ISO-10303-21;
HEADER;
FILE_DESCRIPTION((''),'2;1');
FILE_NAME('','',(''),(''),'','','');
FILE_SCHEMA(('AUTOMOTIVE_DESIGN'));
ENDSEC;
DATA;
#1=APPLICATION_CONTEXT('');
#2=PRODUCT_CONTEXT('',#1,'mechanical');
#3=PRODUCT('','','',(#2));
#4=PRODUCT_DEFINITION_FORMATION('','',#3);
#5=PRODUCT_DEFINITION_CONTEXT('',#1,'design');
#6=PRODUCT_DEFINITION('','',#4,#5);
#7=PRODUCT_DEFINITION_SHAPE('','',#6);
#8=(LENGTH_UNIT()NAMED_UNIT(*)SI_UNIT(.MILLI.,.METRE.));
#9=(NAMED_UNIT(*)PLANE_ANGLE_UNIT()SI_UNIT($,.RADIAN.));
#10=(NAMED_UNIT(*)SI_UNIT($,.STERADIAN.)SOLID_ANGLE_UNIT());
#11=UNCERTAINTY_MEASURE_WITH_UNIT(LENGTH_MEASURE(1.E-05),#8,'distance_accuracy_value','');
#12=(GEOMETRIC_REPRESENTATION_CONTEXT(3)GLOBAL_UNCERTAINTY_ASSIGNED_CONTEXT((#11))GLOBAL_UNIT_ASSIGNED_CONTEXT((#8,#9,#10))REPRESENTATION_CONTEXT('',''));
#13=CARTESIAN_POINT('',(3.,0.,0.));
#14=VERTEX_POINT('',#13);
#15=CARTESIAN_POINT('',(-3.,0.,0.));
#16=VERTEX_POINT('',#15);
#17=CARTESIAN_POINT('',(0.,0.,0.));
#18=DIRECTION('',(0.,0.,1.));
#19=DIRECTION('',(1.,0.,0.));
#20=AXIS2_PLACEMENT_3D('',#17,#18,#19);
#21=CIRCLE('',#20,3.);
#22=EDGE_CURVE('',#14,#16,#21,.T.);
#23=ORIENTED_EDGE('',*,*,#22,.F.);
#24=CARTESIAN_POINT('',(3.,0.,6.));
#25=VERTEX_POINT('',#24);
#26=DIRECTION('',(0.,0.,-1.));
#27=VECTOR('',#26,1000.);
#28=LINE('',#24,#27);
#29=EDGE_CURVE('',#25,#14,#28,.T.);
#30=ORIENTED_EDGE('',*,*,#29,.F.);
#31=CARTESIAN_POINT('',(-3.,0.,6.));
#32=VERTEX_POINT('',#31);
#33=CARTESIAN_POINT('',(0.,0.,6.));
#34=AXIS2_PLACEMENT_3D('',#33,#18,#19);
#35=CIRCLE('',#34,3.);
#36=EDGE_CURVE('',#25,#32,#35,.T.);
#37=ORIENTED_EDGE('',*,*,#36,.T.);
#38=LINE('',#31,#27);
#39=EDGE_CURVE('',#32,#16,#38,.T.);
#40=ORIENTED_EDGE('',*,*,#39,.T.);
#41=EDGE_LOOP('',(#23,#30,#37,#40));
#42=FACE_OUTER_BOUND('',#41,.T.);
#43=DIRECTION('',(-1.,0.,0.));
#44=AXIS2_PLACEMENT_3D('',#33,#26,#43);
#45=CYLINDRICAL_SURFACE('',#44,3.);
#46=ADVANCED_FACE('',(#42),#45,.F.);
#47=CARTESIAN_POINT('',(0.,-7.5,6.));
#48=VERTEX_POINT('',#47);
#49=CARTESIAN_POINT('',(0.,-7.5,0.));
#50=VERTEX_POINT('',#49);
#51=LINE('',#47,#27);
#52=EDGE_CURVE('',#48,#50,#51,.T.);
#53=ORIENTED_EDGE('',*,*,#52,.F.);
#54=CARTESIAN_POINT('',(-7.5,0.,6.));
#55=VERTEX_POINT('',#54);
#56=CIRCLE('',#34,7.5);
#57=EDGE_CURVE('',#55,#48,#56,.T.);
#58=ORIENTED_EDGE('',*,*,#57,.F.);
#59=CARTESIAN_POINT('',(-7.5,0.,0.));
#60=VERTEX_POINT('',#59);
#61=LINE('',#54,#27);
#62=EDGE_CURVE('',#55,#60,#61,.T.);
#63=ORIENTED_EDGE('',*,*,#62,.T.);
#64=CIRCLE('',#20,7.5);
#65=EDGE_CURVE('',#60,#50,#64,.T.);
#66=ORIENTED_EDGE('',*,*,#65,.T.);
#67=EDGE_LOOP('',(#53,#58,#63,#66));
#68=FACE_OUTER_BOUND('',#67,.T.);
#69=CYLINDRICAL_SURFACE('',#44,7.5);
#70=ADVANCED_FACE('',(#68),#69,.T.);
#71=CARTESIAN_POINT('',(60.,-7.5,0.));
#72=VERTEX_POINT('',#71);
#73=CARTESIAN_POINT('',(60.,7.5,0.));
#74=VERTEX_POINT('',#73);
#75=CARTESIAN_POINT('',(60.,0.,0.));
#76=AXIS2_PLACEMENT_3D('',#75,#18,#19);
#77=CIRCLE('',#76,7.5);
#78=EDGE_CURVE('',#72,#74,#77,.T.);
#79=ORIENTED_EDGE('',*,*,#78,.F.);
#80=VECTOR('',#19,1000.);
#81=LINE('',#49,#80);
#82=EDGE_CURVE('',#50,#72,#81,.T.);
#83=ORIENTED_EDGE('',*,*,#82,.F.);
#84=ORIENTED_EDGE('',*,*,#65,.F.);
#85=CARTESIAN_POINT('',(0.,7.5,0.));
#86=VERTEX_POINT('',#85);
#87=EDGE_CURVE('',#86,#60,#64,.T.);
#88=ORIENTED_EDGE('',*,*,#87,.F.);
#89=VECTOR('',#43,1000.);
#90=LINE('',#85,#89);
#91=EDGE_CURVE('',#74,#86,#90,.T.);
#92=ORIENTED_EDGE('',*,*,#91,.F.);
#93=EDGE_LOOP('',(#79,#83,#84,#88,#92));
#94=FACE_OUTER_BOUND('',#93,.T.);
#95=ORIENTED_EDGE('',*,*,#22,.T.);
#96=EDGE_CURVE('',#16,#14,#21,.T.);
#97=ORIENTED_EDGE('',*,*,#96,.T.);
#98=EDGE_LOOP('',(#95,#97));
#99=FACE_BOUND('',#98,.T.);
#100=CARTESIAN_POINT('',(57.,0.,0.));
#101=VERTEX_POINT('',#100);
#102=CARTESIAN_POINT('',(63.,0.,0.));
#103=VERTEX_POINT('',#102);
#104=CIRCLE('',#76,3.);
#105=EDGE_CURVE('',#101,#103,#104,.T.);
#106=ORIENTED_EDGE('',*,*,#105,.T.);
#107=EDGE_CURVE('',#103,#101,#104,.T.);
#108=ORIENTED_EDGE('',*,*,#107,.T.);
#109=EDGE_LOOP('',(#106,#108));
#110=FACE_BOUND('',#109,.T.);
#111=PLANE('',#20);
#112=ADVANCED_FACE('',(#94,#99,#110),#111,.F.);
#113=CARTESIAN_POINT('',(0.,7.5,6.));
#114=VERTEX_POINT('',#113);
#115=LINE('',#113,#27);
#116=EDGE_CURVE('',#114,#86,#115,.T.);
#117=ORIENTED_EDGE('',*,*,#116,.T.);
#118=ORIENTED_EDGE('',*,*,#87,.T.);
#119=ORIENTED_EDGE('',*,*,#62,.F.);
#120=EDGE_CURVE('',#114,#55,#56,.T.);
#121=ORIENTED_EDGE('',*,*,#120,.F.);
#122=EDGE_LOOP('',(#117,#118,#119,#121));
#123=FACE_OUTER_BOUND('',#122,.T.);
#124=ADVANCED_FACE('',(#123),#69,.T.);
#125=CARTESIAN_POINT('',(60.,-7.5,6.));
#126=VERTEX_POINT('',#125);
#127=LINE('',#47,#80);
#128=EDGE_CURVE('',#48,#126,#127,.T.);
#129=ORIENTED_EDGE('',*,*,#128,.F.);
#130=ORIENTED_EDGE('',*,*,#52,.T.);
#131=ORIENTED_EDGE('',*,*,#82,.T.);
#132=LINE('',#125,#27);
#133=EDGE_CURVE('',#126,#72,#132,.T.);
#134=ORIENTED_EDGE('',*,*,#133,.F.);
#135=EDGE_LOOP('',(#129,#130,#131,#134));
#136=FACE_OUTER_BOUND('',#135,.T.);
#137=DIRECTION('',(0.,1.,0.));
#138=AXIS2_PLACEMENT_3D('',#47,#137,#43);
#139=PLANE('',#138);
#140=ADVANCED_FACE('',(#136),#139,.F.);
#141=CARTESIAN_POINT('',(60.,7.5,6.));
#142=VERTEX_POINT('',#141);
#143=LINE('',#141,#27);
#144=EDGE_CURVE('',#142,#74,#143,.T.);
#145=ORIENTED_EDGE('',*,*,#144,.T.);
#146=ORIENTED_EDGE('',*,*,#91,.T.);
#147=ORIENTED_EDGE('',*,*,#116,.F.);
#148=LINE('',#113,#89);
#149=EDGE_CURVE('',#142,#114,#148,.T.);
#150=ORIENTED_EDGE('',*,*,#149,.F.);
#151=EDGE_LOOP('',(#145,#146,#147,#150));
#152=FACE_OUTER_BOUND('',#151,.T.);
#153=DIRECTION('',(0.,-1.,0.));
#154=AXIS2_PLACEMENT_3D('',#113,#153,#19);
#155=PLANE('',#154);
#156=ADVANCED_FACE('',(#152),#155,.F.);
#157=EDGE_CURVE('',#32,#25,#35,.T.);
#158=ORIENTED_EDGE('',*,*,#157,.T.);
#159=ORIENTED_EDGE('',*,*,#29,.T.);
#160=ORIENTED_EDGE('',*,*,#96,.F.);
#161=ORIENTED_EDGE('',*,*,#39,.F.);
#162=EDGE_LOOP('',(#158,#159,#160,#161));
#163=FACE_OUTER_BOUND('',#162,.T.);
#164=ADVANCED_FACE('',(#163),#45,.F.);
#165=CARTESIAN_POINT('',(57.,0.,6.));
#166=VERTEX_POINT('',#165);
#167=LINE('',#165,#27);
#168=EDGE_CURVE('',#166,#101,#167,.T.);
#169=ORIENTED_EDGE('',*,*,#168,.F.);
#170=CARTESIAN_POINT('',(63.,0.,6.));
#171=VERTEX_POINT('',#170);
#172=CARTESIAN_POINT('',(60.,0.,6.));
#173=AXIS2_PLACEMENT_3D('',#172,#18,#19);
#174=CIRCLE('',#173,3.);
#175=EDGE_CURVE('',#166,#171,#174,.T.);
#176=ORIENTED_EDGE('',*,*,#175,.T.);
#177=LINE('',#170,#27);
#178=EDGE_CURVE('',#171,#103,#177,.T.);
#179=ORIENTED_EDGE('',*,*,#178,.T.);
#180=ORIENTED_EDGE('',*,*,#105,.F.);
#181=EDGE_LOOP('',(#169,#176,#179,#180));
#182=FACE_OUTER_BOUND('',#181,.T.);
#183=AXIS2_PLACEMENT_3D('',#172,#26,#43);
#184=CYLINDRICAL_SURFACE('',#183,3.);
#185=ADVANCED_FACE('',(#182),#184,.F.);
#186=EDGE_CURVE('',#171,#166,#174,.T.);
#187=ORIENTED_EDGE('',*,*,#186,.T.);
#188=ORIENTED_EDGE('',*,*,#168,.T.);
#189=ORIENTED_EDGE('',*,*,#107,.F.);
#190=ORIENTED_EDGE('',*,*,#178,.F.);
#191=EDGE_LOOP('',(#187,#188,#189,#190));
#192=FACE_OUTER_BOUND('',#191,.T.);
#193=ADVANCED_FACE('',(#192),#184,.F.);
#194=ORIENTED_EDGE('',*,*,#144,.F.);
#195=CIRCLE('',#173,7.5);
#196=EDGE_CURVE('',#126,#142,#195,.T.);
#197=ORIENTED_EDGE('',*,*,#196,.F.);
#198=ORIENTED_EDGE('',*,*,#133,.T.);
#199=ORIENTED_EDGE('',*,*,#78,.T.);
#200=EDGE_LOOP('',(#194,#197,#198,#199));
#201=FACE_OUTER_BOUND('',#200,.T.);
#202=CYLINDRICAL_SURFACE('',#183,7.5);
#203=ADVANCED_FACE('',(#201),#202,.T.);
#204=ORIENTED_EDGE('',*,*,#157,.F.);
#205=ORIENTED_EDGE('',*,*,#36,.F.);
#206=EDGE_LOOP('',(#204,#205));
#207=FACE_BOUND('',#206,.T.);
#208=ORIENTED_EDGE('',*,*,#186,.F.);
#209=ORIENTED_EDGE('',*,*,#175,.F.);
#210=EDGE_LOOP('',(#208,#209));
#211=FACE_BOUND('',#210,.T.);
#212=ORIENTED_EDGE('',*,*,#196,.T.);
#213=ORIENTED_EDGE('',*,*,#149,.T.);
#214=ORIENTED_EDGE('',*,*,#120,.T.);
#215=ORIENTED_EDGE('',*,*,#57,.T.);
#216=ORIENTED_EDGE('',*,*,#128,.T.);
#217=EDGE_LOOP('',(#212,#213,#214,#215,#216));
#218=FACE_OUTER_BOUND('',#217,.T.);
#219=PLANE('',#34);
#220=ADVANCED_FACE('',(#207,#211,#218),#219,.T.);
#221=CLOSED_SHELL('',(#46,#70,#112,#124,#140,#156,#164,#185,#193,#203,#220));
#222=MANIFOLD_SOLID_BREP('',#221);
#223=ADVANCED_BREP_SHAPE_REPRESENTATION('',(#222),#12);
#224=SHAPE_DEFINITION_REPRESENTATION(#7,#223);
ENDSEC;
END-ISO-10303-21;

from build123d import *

# Parameters (mm, degrees)
SKETCH1_R           = 3
BOSS_EXTRUDE1_DEPTH = 6


with BuildPart() as part:
    # Sketch1 → Boss-Extrude1 (new body)
    with BuildSketch(Plane.XY):
        with BuildLine():
            Line((0, 7.5), (60, 7.5))
            ThreePointArc((60, 7.5), (67.5, 0), (60, -7.5))
            Line((60, -7.5), (0, -7.5))
            ThreePointArc((0, -7.5), (-7.5, 0), (0, 7.5))
        make_face()
        Circle(SKETCH1_R, mode=Mode.SUBTRACT)
        with Locations((60, 0)):
            Circle(SKETCH1_R, mode=Mode.SUBTRACT)
    extrude(amount=BOSS_EXTRUDE1_DEPTH)


solid = part.part
